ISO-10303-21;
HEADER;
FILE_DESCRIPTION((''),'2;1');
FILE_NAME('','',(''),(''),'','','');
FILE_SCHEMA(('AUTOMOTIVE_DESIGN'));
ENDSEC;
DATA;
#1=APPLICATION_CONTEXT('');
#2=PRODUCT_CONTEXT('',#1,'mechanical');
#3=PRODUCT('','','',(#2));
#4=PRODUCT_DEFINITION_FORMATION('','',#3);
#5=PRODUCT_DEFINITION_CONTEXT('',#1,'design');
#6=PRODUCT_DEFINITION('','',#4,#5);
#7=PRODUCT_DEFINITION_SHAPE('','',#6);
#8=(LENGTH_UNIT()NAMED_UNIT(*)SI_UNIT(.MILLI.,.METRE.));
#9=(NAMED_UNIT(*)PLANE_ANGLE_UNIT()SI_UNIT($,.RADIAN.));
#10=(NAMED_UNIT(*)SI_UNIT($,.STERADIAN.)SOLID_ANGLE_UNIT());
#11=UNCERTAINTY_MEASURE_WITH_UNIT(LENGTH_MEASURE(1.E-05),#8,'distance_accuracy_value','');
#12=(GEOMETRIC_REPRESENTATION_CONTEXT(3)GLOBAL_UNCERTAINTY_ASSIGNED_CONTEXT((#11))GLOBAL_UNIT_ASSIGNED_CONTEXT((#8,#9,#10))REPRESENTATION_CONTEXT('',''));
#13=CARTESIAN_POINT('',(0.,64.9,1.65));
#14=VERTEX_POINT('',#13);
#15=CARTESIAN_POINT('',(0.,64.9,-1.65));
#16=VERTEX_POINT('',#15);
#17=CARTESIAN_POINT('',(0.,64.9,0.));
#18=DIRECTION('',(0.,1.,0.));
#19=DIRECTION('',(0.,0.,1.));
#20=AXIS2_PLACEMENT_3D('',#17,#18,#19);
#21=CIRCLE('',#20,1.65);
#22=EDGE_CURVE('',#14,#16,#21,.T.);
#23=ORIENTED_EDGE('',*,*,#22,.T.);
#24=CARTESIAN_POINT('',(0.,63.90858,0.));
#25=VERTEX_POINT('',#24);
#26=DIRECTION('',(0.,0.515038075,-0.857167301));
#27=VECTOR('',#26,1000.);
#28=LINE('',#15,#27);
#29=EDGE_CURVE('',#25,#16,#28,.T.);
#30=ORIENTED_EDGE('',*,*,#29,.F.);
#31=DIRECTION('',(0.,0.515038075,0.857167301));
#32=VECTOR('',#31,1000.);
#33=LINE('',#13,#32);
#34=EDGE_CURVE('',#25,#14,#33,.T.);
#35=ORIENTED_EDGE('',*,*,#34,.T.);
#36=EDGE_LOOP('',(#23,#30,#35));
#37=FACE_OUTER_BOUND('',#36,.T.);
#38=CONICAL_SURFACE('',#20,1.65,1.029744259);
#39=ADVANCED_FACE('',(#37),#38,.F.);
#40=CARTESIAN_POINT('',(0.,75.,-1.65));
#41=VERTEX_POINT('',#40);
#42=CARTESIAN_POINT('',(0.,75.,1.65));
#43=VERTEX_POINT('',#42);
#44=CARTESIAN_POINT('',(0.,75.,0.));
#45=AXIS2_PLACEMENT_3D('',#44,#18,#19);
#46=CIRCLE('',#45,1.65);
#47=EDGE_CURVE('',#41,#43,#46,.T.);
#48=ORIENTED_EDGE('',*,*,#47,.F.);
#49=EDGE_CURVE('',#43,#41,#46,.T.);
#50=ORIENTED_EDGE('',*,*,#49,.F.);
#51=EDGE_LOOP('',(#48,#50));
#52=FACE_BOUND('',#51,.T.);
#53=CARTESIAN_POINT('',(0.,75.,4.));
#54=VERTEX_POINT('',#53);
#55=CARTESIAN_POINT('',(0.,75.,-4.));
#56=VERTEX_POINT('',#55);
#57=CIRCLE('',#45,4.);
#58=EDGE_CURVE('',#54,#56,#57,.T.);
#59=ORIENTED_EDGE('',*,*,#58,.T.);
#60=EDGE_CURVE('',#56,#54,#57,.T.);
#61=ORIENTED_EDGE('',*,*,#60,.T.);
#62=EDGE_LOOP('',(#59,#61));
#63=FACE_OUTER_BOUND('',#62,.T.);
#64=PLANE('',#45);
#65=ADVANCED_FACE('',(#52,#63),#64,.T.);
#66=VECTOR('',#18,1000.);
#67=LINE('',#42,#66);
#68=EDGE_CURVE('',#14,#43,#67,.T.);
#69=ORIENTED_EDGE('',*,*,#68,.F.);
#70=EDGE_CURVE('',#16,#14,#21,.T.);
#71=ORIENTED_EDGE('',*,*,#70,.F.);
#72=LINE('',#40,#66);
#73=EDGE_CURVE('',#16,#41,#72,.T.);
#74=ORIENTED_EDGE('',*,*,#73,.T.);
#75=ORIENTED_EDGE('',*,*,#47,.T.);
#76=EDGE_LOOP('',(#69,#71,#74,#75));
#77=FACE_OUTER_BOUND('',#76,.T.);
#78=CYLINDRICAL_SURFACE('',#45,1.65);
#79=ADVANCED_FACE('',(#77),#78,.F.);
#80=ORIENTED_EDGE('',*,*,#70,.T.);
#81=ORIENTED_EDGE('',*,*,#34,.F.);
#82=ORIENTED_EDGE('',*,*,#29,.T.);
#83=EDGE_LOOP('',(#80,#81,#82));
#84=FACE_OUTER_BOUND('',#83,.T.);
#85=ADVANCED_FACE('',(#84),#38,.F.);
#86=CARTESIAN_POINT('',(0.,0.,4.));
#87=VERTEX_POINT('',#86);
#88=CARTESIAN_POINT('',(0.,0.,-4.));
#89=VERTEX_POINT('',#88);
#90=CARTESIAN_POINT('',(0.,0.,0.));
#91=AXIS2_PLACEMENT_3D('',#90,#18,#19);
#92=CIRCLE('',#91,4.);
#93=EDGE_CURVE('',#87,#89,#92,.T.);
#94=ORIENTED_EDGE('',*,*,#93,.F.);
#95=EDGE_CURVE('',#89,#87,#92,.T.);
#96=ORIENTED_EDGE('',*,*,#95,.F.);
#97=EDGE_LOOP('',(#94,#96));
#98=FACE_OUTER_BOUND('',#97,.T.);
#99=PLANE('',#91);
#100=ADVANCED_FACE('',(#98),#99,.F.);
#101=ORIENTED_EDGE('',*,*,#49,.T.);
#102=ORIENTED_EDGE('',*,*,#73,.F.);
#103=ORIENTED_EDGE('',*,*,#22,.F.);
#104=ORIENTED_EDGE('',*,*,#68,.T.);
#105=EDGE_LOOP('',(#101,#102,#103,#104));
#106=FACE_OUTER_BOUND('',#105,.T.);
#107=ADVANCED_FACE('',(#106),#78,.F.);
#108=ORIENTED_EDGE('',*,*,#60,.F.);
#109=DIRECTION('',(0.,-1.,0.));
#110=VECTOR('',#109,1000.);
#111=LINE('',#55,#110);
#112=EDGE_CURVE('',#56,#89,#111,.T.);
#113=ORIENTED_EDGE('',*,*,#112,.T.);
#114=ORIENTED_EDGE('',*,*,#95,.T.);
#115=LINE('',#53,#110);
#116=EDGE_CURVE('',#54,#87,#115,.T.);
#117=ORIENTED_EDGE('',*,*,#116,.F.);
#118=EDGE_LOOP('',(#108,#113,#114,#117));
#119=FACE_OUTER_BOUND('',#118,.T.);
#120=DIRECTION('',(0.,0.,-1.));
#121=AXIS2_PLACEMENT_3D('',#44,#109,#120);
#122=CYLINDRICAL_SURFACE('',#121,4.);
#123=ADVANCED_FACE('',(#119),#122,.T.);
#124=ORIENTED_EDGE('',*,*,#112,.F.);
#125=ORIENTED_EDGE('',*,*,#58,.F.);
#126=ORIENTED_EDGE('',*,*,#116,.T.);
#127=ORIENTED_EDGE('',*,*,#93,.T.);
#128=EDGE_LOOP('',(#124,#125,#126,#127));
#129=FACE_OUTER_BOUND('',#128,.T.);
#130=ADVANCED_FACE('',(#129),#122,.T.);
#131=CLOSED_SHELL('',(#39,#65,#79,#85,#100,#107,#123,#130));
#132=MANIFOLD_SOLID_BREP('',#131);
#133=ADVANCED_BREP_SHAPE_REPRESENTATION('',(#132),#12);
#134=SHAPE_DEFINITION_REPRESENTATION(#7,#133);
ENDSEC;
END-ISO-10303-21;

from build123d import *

# Parameters (mm, degrees)
SKETCH_1_R             = 4
EXTRUDE_1_DEPTH        = 75
HOLE_WIZARD_M4_1_D     = 3.3
HOLE_WIZARD_M4_1_DEPTH = 10.1
HOLE_WIZARD_M4_1_TIP   = 0.991420021


with BuildPart() as part:
    # 草图1 → 凸台-拉伸1 (new body)
    with BuildSketch(Plane(origin=(0, 0, 0), x_dir=(1, 0, 0), z_dir=(0, 1, 0))):
        with Locations(Location((0, 0, 0), (0, 0, 270))):
            Circle(SKETCH_1_R)
    extrude(amount=EXTRUDE_1_DEPTH)

    # M4 螺纹孔1
    with Locations(Plane(origin=(0, 75, 0), x_dir=(1, 0, 0), z_dir=(0, 1, 0))):
        with Locations((0, 0)):
            Hole(HOLE_WIZARD_M4_1_D / 2, depth=HOLE_WIZARD_M4_1_DEPTH)
            with Locations((0, 0, -(HOLE_WIZARD_M4_1_DEPTH + HOLE_WIZARD_M4_1_TIP / 2))):  # 118° drill point
                Cone(0, HOLE_WIZARD_M4_1_D / 2, HOLE_WIZARD_M4_1_TIP, mode=Mode.SUBTRACT)


solid = part.part
